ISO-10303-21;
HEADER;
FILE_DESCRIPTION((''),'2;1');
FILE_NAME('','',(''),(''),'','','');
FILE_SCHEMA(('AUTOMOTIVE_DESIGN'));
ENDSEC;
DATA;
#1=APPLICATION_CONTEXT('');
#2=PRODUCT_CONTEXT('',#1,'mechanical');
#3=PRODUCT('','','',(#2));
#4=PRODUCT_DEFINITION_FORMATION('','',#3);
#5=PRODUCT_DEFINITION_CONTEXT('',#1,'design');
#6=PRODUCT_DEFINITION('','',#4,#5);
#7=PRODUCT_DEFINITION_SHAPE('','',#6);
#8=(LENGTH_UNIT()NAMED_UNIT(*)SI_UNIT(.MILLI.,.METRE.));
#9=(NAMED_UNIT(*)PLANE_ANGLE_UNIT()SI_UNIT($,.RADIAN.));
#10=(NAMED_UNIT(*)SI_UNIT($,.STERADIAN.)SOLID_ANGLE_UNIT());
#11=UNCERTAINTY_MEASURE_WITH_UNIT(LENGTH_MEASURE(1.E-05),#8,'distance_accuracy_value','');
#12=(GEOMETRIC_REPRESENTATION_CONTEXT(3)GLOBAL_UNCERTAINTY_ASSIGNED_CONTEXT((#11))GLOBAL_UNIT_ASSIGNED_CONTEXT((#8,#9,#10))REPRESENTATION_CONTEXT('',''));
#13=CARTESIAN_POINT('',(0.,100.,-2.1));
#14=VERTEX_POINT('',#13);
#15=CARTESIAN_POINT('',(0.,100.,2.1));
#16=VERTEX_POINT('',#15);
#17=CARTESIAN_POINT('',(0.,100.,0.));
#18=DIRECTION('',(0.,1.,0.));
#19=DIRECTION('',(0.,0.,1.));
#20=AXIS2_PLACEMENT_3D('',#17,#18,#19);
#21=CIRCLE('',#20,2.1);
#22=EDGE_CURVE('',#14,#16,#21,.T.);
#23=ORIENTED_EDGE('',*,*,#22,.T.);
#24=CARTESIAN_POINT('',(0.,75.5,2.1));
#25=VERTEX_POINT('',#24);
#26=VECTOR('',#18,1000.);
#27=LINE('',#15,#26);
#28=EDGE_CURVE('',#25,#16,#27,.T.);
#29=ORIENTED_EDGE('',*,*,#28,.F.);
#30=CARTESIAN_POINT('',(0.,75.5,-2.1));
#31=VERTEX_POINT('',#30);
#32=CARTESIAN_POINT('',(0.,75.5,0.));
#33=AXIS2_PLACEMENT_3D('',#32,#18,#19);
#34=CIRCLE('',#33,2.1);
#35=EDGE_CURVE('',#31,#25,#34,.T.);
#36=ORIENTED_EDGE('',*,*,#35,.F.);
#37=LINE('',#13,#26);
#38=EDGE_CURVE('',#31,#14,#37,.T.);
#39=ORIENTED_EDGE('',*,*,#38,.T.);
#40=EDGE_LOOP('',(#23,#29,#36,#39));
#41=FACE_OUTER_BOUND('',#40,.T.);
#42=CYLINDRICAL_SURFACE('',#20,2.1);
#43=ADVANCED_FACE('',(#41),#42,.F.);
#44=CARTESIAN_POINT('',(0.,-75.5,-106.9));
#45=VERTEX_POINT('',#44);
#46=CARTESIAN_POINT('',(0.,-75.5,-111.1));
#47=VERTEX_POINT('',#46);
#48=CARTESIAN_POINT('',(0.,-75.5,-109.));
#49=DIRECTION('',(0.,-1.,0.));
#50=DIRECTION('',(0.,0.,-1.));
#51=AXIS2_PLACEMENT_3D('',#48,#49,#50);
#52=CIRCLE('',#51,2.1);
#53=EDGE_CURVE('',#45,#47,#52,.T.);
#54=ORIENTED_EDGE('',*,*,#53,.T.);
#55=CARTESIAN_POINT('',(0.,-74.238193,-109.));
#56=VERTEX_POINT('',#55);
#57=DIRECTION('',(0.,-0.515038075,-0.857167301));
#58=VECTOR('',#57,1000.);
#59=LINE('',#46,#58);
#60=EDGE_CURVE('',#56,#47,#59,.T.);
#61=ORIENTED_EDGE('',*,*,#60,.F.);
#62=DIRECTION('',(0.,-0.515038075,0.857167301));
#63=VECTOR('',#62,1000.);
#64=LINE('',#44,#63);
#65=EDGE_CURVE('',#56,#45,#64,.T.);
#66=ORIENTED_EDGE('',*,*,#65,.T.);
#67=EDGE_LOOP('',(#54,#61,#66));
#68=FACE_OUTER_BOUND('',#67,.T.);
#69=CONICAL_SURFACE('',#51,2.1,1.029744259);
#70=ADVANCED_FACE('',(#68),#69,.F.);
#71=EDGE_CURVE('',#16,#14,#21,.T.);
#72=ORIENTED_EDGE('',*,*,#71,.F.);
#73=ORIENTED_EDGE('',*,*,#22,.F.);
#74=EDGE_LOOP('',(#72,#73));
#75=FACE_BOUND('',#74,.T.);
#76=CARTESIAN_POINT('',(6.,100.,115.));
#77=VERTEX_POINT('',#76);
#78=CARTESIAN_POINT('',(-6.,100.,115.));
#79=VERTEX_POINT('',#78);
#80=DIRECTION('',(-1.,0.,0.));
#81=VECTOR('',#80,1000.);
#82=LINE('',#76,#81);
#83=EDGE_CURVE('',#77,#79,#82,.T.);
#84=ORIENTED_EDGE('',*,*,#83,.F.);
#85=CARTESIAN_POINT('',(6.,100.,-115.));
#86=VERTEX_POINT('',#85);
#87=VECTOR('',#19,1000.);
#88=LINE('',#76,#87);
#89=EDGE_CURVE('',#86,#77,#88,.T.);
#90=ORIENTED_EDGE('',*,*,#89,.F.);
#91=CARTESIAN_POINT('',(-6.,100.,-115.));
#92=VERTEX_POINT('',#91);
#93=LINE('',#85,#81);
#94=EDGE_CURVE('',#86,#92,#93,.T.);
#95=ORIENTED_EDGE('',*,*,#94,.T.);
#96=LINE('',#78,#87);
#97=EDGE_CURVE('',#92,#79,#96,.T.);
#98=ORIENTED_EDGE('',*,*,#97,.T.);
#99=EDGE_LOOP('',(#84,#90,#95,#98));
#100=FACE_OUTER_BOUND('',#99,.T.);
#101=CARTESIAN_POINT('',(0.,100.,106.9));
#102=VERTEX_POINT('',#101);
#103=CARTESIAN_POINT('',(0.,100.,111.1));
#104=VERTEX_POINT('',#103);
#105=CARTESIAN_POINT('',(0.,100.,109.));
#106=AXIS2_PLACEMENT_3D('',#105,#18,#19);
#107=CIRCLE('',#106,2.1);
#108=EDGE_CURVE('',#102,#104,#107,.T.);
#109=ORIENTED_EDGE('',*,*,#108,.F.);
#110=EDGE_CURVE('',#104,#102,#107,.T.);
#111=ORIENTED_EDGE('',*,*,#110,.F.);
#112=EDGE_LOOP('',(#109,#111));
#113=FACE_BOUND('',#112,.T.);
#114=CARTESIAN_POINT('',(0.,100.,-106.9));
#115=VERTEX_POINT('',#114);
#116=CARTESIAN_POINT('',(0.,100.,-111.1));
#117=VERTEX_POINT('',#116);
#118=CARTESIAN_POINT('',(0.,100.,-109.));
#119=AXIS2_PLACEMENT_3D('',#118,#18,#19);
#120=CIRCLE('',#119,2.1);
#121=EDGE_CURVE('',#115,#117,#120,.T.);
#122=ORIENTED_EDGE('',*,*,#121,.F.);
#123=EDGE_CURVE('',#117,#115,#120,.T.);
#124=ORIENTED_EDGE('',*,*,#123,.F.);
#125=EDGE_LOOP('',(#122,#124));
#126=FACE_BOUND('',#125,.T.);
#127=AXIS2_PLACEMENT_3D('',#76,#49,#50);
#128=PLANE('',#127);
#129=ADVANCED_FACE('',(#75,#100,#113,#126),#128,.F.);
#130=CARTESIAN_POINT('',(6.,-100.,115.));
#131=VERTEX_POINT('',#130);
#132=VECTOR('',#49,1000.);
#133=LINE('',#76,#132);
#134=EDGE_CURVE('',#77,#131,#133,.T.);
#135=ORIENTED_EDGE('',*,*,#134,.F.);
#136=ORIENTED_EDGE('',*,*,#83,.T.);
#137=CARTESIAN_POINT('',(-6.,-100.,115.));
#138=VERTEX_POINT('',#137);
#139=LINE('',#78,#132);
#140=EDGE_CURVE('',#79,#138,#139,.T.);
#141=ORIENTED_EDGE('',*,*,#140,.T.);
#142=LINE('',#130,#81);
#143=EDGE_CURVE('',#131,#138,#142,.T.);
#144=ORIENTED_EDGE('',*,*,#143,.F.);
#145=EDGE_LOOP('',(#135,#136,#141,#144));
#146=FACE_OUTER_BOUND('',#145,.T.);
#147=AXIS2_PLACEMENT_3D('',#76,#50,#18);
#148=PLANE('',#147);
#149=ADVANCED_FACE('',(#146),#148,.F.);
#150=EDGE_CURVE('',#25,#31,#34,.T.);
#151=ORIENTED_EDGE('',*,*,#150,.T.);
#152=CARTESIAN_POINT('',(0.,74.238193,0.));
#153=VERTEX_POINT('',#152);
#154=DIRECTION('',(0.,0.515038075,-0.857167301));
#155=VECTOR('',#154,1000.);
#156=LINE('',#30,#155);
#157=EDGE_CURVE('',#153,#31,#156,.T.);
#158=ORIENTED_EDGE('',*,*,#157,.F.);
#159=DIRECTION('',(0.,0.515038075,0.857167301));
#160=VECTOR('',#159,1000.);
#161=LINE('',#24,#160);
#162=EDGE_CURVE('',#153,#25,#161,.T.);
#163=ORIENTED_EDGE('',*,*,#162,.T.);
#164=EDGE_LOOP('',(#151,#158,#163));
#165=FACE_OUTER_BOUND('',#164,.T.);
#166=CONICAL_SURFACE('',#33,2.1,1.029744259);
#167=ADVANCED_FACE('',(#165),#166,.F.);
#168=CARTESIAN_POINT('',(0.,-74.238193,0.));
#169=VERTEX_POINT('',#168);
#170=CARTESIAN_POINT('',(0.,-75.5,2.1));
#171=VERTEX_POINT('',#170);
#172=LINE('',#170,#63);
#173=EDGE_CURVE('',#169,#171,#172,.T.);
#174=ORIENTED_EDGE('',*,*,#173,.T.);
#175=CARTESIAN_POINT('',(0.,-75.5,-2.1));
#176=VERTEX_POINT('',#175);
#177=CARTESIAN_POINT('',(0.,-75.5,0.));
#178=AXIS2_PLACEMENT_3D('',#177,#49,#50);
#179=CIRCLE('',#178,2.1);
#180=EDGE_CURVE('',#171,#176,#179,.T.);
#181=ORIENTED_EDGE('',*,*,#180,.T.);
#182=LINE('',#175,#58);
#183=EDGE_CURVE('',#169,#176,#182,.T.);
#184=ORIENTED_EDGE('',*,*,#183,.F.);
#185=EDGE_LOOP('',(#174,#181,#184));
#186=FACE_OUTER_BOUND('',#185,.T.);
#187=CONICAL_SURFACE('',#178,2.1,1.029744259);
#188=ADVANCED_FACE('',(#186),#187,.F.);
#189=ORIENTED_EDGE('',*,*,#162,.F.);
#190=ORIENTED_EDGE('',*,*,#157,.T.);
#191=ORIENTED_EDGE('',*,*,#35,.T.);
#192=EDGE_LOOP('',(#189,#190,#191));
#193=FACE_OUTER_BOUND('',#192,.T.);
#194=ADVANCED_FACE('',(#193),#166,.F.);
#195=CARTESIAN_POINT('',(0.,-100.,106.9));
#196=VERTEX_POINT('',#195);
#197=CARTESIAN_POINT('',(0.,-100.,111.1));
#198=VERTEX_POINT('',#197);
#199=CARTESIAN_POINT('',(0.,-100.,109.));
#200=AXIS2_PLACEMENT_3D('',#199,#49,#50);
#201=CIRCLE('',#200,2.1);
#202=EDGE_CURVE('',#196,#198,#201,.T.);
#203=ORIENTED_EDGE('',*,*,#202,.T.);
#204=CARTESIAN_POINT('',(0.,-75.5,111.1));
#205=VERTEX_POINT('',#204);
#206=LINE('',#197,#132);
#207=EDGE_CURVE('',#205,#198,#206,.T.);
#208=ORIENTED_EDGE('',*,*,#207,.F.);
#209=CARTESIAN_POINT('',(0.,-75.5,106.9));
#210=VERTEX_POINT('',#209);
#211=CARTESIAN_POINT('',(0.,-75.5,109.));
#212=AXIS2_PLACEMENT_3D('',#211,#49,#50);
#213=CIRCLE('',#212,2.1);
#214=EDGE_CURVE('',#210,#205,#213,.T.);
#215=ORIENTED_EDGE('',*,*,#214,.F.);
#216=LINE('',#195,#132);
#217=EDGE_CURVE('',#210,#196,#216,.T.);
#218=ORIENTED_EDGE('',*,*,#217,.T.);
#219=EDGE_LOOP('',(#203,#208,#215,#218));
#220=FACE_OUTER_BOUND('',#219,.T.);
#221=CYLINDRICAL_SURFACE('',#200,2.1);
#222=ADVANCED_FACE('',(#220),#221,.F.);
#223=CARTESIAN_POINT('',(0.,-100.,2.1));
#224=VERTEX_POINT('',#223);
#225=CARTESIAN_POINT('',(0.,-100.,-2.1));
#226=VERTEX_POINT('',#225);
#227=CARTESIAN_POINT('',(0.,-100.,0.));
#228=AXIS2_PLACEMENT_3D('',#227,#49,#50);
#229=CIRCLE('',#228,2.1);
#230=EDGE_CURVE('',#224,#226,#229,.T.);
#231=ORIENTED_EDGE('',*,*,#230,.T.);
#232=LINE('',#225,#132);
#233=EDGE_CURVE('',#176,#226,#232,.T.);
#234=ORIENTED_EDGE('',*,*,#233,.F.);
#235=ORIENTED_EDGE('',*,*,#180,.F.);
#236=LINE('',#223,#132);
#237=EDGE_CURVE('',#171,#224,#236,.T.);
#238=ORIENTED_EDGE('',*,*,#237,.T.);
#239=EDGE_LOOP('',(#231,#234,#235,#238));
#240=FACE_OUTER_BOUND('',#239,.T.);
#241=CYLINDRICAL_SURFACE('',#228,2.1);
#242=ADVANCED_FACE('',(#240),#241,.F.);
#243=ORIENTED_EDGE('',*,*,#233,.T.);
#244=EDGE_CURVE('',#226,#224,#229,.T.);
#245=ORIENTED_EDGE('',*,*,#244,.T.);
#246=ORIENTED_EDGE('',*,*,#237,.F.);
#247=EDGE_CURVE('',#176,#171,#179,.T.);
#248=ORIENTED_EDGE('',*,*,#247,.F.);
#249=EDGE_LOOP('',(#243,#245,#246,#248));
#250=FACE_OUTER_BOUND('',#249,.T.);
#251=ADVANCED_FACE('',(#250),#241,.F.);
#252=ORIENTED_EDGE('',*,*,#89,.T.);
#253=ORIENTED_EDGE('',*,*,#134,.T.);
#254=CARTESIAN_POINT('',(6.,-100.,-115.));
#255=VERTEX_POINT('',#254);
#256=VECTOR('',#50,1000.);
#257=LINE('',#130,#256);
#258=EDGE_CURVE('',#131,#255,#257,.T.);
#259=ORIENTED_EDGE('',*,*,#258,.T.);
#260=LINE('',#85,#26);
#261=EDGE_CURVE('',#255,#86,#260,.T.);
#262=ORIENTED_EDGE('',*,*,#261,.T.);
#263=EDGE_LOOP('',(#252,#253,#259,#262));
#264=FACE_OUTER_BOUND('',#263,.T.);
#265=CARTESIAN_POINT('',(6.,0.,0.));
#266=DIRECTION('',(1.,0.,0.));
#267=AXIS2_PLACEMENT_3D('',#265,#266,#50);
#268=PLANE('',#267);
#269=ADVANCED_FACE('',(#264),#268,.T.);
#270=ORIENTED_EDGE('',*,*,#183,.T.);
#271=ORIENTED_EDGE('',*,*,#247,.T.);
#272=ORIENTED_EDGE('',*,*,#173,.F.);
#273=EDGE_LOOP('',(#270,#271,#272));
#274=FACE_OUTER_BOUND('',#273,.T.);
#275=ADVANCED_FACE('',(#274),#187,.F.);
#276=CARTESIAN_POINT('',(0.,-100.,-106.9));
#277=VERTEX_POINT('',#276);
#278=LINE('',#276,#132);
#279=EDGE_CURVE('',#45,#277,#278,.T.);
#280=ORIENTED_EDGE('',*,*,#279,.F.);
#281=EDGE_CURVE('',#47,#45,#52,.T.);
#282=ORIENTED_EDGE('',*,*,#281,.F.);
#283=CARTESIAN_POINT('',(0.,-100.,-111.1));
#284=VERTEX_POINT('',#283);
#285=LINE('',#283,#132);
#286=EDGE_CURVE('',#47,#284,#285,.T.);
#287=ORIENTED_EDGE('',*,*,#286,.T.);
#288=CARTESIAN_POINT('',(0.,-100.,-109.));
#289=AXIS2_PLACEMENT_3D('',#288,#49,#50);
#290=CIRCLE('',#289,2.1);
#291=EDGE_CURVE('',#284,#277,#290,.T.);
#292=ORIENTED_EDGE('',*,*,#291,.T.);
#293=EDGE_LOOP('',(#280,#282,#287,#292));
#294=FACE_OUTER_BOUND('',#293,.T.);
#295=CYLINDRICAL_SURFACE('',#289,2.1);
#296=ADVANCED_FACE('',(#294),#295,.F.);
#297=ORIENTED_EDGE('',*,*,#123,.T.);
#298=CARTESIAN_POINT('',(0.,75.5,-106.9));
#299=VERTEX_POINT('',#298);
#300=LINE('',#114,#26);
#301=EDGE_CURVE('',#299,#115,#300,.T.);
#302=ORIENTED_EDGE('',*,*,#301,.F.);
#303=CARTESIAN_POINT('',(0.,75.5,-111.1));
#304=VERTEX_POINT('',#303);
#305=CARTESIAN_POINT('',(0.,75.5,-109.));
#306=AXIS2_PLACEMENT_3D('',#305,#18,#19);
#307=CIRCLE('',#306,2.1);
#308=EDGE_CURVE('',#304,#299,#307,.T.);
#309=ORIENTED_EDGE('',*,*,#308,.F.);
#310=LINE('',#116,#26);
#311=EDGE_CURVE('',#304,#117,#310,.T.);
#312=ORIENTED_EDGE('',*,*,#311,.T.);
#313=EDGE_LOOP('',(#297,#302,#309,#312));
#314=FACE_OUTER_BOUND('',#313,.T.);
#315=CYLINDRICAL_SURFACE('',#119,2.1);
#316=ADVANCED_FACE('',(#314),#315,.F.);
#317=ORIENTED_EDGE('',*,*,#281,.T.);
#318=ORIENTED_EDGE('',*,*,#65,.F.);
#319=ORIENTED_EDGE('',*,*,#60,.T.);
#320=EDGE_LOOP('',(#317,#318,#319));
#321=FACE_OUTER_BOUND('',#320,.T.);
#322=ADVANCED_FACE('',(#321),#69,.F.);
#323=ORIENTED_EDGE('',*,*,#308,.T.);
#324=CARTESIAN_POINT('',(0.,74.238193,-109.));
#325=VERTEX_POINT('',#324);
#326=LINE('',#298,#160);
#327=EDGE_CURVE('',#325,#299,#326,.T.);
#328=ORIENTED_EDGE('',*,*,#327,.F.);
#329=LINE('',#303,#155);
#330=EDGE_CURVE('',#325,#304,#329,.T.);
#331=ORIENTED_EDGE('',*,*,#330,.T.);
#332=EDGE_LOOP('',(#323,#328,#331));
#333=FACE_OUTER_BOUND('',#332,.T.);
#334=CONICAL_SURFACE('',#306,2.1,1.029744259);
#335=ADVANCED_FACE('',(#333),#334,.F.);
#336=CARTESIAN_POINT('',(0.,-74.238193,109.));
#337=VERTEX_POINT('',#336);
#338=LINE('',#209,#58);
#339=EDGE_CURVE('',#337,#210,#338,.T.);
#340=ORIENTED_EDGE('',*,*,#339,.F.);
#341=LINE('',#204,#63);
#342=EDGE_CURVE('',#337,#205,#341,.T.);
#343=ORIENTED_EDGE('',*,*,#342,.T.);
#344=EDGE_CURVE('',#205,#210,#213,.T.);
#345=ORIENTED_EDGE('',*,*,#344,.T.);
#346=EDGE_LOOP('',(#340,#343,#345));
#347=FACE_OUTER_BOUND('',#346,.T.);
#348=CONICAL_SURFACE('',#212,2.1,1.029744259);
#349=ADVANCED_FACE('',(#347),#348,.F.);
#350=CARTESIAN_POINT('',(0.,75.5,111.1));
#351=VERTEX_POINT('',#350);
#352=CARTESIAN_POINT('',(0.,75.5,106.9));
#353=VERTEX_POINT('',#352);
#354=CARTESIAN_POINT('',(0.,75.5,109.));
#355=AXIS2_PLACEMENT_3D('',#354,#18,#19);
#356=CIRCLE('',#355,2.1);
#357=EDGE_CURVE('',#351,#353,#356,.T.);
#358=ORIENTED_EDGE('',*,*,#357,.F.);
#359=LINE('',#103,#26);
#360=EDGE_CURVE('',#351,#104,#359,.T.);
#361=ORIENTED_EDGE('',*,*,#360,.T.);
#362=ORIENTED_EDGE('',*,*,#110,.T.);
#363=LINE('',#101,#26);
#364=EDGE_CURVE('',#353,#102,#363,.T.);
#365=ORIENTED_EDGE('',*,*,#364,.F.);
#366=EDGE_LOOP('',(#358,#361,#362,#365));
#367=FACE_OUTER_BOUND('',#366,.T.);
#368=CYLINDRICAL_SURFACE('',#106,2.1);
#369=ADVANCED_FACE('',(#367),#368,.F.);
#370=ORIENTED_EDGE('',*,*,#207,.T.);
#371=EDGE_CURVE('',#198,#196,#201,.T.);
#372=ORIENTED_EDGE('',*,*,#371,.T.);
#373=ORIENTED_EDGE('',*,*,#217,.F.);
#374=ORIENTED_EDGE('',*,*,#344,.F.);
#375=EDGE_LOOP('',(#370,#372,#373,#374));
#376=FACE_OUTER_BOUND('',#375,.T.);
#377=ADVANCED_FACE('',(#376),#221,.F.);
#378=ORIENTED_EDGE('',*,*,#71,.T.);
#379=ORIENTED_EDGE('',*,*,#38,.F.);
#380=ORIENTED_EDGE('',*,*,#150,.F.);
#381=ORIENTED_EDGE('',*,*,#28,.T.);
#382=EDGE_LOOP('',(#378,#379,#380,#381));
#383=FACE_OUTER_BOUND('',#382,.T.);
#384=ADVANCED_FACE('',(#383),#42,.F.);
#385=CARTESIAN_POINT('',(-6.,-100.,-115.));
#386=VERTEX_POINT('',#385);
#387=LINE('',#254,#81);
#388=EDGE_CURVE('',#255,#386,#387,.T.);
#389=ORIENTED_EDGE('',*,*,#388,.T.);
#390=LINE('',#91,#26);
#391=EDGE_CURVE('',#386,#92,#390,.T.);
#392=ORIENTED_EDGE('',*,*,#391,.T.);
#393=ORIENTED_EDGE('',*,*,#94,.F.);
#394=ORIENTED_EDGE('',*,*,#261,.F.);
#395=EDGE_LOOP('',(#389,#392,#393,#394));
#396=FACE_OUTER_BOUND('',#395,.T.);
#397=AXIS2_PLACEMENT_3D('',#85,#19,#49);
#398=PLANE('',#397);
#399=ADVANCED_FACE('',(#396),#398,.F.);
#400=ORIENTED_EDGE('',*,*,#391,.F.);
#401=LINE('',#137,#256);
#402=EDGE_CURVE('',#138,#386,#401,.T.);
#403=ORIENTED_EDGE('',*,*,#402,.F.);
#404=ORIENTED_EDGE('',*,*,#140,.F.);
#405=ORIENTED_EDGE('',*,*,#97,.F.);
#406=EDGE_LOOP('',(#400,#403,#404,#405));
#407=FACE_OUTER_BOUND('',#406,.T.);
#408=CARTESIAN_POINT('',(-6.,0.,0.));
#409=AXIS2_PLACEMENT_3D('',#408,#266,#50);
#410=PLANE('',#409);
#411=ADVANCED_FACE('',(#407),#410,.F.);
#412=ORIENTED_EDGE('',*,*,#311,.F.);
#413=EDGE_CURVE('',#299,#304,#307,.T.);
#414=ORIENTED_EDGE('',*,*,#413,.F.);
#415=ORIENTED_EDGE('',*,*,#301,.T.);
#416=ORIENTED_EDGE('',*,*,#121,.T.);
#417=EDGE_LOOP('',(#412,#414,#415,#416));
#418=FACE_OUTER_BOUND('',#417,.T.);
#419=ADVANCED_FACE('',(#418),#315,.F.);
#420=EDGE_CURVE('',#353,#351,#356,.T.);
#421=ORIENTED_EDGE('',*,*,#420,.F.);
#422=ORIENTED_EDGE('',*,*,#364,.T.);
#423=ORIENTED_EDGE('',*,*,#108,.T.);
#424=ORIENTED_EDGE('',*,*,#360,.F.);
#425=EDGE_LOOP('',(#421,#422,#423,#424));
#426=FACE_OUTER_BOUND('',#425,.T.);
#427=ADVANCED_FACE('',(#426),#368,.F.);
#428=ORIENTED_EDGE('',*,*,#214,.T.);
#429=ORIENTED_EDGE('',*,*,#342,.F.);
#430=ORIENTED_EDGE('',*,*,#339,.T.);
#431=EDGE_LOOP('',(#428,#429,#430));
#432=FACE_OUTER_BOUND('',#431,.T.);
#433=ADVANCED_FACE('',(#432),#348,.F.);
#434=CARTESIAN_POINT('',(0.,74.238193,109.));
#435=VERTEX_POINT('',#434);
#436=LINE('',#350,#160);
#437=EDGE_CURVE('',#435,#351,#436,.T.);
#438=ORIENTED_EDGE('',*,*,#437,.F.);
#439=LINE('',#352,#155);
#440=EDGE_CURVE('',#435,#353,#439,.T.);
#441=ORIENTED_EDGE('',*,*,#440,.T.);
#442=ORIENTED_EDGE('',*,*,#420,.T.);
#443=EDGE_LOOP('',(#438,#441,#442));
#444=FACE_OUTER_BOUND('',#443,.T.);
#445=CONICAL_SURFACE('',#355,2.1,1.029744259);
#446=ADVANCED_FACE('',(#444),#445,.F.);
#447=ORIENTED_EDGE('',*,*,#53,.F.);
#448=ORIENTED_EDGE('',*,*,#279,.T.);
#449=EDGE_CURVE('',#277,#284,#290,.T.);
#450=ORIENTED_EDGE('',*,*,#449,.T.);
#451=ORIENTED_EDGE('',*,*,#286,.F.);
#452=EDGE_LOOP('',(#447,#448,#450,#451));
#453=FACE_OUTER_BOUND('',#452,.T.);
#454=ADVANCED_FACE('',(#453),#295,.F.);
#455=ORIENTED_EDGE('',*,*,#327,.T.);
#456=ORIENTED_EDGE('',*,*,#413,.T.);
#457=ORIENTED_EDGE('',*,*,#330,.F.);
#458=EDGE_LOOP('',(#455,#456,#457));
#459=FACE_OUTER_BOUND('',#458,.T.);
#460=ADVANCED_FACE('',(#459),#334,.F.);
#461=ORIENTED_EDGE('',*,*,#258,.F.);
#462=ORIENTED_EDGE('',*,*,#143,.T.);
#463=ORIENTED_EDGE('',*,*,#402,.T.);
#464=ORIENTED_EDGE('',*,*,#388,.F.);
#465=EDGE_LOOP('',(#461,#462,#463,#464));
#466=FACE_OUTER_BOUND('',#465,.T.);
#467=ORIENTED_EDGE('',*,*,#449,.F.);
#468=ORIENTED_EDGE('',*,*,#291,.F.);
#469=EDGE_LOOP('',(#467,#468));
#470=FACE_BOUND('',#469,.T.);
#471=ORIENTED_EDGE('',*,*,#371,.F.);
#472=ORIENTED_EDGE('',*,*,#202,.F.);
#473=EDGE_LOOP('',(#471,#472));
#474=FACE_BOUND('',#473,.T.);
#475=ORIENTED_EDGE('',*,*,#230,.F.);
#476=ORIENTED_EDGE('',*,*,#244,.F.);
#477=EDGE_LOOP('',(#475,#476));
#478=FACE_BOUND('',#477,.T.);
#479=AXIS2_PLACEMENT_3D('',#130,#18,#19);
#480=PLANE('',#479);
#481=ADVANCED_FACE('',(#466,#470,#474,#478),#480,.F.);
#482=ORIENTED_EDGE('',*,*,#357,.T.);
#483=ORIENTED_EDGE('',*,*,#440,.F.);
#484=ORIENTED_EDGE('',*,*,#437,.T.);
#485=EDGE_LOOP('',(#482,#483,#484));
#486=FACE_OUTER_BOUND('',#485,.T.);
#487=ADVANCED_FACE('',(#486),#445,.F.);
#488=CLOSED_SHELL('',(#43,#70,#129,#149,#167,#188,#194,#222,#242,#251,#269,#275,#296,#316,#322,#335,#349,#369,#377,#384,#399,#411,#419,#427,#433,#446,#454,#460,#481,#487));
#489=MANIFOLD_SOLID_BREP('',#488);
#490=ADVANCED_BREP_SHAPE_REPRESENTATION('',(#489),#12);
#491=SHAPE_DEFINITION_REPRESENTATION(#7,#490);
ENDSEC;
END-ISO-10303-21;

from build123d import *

# Parameters (mm, degrees)
SKETCH1_W                  = 230
SKETCH1_H                  = 200
BOSS_EXTRUDE1_DEPTH        = 6
M5_TAPPED_HOLE1_AT_2_COUNT = 2
M5_TAPPED_HOLE1_AT_2_PITCH = 109
M5_TAPPED_HOLE1_AT_3_COUNT = 2
M5_TAPPED_HOLE1_AT_3_PITCH = 218


with BuildPart() as part:
    # Sketch1 → Boss-Extrude1 (new, symmetric)
    with BuildSketch(Plane(origin=(0, 0, 0), x_dir=(0, 0, -1), z_dir=(1, 0, 0))):
        Rectangle(SKETCH1_W, SKETCH1_H)
    extrude(amount=BOSS_EXTRUDE1_DEPTH, both=True)

    # Sketch3 → M5 Tapped Hole1 (revolve, cut)
    with BuildSketch(Plane(origin=(0, 100, -109), x_dir=(0, 0, 1), z_dir=(1, 0, 0))):
        Polygon((0, 0), (0, 25.7618073), (2.1, 24.5), (2.1, 0), align=None)
    m5_tapped_hole1 = revolve(axis=Axis((0, 106.35, -109), (0, -1, 0)), mode=Mode.SUBTRACT)

    # M5 Tapped Hole1 at 2: M5 Tapped Hole1 ×2
    with Locations(*[(0, 0, i * M5_TAPPED_HOLE1_AT_2_PITCH) for i in range(1, M5_TAPPED_HOLE1_AT_2_COUNT)]):
        add(m5_tapped_hole1, mode=Mode.SUBTRACT)

    # M5 Tapped Hole1 at 3: M5 Tapped Hole1 ×2
    with Locations(*[(0, 0, i * M5_TAPPED_HOLE1_AT_3_PITCH) for i in range(1, M5_TAPPED_HOLE1_AT_3_COUNT)]):
        add(m5_tapped_hole1, mode=Mode.SUBTRACT)

    # Mirror1: M5 Tapped Hole1 across plane
    add(m5_tapped_hole1.mirror(Plane.ZX), mode=Mode.SUBTRACT)

    # Mirror1 copy 1 sketch → Mirror1 copy 1 (revolve, cut)
    with BuildSketch(Plane(origin=(0, -100, 0), x_dir=(0, 0, 1), z_dir=(1, 0, 0))):
        Polygon((0, 0), (0, -25.7618073), (2.1, -24.5), (2.1, 0), align=None)
    revolve(axis=Axis((0, -106.35, 0), (0, -1, 0)), mode=Mode.SUBTRACT)

    # Mirror1 copy 2 sketch → Mirror1 copy 2 (revolve, cut)
    with BuildSketch(Plane(origin=(0, -100, 109), x_dir=(0, 0, 1), z_dir=(1, 0, 0))):
        Polygon((0, 0), (0, -25.7618073), (2.1, -24.5), (2.1, 0), align=None)
    revolve(axis=Axis((0, -106.35, 109), (0, -1, 0)), mode=Mode.SUBTRACT)


solid = part.part
